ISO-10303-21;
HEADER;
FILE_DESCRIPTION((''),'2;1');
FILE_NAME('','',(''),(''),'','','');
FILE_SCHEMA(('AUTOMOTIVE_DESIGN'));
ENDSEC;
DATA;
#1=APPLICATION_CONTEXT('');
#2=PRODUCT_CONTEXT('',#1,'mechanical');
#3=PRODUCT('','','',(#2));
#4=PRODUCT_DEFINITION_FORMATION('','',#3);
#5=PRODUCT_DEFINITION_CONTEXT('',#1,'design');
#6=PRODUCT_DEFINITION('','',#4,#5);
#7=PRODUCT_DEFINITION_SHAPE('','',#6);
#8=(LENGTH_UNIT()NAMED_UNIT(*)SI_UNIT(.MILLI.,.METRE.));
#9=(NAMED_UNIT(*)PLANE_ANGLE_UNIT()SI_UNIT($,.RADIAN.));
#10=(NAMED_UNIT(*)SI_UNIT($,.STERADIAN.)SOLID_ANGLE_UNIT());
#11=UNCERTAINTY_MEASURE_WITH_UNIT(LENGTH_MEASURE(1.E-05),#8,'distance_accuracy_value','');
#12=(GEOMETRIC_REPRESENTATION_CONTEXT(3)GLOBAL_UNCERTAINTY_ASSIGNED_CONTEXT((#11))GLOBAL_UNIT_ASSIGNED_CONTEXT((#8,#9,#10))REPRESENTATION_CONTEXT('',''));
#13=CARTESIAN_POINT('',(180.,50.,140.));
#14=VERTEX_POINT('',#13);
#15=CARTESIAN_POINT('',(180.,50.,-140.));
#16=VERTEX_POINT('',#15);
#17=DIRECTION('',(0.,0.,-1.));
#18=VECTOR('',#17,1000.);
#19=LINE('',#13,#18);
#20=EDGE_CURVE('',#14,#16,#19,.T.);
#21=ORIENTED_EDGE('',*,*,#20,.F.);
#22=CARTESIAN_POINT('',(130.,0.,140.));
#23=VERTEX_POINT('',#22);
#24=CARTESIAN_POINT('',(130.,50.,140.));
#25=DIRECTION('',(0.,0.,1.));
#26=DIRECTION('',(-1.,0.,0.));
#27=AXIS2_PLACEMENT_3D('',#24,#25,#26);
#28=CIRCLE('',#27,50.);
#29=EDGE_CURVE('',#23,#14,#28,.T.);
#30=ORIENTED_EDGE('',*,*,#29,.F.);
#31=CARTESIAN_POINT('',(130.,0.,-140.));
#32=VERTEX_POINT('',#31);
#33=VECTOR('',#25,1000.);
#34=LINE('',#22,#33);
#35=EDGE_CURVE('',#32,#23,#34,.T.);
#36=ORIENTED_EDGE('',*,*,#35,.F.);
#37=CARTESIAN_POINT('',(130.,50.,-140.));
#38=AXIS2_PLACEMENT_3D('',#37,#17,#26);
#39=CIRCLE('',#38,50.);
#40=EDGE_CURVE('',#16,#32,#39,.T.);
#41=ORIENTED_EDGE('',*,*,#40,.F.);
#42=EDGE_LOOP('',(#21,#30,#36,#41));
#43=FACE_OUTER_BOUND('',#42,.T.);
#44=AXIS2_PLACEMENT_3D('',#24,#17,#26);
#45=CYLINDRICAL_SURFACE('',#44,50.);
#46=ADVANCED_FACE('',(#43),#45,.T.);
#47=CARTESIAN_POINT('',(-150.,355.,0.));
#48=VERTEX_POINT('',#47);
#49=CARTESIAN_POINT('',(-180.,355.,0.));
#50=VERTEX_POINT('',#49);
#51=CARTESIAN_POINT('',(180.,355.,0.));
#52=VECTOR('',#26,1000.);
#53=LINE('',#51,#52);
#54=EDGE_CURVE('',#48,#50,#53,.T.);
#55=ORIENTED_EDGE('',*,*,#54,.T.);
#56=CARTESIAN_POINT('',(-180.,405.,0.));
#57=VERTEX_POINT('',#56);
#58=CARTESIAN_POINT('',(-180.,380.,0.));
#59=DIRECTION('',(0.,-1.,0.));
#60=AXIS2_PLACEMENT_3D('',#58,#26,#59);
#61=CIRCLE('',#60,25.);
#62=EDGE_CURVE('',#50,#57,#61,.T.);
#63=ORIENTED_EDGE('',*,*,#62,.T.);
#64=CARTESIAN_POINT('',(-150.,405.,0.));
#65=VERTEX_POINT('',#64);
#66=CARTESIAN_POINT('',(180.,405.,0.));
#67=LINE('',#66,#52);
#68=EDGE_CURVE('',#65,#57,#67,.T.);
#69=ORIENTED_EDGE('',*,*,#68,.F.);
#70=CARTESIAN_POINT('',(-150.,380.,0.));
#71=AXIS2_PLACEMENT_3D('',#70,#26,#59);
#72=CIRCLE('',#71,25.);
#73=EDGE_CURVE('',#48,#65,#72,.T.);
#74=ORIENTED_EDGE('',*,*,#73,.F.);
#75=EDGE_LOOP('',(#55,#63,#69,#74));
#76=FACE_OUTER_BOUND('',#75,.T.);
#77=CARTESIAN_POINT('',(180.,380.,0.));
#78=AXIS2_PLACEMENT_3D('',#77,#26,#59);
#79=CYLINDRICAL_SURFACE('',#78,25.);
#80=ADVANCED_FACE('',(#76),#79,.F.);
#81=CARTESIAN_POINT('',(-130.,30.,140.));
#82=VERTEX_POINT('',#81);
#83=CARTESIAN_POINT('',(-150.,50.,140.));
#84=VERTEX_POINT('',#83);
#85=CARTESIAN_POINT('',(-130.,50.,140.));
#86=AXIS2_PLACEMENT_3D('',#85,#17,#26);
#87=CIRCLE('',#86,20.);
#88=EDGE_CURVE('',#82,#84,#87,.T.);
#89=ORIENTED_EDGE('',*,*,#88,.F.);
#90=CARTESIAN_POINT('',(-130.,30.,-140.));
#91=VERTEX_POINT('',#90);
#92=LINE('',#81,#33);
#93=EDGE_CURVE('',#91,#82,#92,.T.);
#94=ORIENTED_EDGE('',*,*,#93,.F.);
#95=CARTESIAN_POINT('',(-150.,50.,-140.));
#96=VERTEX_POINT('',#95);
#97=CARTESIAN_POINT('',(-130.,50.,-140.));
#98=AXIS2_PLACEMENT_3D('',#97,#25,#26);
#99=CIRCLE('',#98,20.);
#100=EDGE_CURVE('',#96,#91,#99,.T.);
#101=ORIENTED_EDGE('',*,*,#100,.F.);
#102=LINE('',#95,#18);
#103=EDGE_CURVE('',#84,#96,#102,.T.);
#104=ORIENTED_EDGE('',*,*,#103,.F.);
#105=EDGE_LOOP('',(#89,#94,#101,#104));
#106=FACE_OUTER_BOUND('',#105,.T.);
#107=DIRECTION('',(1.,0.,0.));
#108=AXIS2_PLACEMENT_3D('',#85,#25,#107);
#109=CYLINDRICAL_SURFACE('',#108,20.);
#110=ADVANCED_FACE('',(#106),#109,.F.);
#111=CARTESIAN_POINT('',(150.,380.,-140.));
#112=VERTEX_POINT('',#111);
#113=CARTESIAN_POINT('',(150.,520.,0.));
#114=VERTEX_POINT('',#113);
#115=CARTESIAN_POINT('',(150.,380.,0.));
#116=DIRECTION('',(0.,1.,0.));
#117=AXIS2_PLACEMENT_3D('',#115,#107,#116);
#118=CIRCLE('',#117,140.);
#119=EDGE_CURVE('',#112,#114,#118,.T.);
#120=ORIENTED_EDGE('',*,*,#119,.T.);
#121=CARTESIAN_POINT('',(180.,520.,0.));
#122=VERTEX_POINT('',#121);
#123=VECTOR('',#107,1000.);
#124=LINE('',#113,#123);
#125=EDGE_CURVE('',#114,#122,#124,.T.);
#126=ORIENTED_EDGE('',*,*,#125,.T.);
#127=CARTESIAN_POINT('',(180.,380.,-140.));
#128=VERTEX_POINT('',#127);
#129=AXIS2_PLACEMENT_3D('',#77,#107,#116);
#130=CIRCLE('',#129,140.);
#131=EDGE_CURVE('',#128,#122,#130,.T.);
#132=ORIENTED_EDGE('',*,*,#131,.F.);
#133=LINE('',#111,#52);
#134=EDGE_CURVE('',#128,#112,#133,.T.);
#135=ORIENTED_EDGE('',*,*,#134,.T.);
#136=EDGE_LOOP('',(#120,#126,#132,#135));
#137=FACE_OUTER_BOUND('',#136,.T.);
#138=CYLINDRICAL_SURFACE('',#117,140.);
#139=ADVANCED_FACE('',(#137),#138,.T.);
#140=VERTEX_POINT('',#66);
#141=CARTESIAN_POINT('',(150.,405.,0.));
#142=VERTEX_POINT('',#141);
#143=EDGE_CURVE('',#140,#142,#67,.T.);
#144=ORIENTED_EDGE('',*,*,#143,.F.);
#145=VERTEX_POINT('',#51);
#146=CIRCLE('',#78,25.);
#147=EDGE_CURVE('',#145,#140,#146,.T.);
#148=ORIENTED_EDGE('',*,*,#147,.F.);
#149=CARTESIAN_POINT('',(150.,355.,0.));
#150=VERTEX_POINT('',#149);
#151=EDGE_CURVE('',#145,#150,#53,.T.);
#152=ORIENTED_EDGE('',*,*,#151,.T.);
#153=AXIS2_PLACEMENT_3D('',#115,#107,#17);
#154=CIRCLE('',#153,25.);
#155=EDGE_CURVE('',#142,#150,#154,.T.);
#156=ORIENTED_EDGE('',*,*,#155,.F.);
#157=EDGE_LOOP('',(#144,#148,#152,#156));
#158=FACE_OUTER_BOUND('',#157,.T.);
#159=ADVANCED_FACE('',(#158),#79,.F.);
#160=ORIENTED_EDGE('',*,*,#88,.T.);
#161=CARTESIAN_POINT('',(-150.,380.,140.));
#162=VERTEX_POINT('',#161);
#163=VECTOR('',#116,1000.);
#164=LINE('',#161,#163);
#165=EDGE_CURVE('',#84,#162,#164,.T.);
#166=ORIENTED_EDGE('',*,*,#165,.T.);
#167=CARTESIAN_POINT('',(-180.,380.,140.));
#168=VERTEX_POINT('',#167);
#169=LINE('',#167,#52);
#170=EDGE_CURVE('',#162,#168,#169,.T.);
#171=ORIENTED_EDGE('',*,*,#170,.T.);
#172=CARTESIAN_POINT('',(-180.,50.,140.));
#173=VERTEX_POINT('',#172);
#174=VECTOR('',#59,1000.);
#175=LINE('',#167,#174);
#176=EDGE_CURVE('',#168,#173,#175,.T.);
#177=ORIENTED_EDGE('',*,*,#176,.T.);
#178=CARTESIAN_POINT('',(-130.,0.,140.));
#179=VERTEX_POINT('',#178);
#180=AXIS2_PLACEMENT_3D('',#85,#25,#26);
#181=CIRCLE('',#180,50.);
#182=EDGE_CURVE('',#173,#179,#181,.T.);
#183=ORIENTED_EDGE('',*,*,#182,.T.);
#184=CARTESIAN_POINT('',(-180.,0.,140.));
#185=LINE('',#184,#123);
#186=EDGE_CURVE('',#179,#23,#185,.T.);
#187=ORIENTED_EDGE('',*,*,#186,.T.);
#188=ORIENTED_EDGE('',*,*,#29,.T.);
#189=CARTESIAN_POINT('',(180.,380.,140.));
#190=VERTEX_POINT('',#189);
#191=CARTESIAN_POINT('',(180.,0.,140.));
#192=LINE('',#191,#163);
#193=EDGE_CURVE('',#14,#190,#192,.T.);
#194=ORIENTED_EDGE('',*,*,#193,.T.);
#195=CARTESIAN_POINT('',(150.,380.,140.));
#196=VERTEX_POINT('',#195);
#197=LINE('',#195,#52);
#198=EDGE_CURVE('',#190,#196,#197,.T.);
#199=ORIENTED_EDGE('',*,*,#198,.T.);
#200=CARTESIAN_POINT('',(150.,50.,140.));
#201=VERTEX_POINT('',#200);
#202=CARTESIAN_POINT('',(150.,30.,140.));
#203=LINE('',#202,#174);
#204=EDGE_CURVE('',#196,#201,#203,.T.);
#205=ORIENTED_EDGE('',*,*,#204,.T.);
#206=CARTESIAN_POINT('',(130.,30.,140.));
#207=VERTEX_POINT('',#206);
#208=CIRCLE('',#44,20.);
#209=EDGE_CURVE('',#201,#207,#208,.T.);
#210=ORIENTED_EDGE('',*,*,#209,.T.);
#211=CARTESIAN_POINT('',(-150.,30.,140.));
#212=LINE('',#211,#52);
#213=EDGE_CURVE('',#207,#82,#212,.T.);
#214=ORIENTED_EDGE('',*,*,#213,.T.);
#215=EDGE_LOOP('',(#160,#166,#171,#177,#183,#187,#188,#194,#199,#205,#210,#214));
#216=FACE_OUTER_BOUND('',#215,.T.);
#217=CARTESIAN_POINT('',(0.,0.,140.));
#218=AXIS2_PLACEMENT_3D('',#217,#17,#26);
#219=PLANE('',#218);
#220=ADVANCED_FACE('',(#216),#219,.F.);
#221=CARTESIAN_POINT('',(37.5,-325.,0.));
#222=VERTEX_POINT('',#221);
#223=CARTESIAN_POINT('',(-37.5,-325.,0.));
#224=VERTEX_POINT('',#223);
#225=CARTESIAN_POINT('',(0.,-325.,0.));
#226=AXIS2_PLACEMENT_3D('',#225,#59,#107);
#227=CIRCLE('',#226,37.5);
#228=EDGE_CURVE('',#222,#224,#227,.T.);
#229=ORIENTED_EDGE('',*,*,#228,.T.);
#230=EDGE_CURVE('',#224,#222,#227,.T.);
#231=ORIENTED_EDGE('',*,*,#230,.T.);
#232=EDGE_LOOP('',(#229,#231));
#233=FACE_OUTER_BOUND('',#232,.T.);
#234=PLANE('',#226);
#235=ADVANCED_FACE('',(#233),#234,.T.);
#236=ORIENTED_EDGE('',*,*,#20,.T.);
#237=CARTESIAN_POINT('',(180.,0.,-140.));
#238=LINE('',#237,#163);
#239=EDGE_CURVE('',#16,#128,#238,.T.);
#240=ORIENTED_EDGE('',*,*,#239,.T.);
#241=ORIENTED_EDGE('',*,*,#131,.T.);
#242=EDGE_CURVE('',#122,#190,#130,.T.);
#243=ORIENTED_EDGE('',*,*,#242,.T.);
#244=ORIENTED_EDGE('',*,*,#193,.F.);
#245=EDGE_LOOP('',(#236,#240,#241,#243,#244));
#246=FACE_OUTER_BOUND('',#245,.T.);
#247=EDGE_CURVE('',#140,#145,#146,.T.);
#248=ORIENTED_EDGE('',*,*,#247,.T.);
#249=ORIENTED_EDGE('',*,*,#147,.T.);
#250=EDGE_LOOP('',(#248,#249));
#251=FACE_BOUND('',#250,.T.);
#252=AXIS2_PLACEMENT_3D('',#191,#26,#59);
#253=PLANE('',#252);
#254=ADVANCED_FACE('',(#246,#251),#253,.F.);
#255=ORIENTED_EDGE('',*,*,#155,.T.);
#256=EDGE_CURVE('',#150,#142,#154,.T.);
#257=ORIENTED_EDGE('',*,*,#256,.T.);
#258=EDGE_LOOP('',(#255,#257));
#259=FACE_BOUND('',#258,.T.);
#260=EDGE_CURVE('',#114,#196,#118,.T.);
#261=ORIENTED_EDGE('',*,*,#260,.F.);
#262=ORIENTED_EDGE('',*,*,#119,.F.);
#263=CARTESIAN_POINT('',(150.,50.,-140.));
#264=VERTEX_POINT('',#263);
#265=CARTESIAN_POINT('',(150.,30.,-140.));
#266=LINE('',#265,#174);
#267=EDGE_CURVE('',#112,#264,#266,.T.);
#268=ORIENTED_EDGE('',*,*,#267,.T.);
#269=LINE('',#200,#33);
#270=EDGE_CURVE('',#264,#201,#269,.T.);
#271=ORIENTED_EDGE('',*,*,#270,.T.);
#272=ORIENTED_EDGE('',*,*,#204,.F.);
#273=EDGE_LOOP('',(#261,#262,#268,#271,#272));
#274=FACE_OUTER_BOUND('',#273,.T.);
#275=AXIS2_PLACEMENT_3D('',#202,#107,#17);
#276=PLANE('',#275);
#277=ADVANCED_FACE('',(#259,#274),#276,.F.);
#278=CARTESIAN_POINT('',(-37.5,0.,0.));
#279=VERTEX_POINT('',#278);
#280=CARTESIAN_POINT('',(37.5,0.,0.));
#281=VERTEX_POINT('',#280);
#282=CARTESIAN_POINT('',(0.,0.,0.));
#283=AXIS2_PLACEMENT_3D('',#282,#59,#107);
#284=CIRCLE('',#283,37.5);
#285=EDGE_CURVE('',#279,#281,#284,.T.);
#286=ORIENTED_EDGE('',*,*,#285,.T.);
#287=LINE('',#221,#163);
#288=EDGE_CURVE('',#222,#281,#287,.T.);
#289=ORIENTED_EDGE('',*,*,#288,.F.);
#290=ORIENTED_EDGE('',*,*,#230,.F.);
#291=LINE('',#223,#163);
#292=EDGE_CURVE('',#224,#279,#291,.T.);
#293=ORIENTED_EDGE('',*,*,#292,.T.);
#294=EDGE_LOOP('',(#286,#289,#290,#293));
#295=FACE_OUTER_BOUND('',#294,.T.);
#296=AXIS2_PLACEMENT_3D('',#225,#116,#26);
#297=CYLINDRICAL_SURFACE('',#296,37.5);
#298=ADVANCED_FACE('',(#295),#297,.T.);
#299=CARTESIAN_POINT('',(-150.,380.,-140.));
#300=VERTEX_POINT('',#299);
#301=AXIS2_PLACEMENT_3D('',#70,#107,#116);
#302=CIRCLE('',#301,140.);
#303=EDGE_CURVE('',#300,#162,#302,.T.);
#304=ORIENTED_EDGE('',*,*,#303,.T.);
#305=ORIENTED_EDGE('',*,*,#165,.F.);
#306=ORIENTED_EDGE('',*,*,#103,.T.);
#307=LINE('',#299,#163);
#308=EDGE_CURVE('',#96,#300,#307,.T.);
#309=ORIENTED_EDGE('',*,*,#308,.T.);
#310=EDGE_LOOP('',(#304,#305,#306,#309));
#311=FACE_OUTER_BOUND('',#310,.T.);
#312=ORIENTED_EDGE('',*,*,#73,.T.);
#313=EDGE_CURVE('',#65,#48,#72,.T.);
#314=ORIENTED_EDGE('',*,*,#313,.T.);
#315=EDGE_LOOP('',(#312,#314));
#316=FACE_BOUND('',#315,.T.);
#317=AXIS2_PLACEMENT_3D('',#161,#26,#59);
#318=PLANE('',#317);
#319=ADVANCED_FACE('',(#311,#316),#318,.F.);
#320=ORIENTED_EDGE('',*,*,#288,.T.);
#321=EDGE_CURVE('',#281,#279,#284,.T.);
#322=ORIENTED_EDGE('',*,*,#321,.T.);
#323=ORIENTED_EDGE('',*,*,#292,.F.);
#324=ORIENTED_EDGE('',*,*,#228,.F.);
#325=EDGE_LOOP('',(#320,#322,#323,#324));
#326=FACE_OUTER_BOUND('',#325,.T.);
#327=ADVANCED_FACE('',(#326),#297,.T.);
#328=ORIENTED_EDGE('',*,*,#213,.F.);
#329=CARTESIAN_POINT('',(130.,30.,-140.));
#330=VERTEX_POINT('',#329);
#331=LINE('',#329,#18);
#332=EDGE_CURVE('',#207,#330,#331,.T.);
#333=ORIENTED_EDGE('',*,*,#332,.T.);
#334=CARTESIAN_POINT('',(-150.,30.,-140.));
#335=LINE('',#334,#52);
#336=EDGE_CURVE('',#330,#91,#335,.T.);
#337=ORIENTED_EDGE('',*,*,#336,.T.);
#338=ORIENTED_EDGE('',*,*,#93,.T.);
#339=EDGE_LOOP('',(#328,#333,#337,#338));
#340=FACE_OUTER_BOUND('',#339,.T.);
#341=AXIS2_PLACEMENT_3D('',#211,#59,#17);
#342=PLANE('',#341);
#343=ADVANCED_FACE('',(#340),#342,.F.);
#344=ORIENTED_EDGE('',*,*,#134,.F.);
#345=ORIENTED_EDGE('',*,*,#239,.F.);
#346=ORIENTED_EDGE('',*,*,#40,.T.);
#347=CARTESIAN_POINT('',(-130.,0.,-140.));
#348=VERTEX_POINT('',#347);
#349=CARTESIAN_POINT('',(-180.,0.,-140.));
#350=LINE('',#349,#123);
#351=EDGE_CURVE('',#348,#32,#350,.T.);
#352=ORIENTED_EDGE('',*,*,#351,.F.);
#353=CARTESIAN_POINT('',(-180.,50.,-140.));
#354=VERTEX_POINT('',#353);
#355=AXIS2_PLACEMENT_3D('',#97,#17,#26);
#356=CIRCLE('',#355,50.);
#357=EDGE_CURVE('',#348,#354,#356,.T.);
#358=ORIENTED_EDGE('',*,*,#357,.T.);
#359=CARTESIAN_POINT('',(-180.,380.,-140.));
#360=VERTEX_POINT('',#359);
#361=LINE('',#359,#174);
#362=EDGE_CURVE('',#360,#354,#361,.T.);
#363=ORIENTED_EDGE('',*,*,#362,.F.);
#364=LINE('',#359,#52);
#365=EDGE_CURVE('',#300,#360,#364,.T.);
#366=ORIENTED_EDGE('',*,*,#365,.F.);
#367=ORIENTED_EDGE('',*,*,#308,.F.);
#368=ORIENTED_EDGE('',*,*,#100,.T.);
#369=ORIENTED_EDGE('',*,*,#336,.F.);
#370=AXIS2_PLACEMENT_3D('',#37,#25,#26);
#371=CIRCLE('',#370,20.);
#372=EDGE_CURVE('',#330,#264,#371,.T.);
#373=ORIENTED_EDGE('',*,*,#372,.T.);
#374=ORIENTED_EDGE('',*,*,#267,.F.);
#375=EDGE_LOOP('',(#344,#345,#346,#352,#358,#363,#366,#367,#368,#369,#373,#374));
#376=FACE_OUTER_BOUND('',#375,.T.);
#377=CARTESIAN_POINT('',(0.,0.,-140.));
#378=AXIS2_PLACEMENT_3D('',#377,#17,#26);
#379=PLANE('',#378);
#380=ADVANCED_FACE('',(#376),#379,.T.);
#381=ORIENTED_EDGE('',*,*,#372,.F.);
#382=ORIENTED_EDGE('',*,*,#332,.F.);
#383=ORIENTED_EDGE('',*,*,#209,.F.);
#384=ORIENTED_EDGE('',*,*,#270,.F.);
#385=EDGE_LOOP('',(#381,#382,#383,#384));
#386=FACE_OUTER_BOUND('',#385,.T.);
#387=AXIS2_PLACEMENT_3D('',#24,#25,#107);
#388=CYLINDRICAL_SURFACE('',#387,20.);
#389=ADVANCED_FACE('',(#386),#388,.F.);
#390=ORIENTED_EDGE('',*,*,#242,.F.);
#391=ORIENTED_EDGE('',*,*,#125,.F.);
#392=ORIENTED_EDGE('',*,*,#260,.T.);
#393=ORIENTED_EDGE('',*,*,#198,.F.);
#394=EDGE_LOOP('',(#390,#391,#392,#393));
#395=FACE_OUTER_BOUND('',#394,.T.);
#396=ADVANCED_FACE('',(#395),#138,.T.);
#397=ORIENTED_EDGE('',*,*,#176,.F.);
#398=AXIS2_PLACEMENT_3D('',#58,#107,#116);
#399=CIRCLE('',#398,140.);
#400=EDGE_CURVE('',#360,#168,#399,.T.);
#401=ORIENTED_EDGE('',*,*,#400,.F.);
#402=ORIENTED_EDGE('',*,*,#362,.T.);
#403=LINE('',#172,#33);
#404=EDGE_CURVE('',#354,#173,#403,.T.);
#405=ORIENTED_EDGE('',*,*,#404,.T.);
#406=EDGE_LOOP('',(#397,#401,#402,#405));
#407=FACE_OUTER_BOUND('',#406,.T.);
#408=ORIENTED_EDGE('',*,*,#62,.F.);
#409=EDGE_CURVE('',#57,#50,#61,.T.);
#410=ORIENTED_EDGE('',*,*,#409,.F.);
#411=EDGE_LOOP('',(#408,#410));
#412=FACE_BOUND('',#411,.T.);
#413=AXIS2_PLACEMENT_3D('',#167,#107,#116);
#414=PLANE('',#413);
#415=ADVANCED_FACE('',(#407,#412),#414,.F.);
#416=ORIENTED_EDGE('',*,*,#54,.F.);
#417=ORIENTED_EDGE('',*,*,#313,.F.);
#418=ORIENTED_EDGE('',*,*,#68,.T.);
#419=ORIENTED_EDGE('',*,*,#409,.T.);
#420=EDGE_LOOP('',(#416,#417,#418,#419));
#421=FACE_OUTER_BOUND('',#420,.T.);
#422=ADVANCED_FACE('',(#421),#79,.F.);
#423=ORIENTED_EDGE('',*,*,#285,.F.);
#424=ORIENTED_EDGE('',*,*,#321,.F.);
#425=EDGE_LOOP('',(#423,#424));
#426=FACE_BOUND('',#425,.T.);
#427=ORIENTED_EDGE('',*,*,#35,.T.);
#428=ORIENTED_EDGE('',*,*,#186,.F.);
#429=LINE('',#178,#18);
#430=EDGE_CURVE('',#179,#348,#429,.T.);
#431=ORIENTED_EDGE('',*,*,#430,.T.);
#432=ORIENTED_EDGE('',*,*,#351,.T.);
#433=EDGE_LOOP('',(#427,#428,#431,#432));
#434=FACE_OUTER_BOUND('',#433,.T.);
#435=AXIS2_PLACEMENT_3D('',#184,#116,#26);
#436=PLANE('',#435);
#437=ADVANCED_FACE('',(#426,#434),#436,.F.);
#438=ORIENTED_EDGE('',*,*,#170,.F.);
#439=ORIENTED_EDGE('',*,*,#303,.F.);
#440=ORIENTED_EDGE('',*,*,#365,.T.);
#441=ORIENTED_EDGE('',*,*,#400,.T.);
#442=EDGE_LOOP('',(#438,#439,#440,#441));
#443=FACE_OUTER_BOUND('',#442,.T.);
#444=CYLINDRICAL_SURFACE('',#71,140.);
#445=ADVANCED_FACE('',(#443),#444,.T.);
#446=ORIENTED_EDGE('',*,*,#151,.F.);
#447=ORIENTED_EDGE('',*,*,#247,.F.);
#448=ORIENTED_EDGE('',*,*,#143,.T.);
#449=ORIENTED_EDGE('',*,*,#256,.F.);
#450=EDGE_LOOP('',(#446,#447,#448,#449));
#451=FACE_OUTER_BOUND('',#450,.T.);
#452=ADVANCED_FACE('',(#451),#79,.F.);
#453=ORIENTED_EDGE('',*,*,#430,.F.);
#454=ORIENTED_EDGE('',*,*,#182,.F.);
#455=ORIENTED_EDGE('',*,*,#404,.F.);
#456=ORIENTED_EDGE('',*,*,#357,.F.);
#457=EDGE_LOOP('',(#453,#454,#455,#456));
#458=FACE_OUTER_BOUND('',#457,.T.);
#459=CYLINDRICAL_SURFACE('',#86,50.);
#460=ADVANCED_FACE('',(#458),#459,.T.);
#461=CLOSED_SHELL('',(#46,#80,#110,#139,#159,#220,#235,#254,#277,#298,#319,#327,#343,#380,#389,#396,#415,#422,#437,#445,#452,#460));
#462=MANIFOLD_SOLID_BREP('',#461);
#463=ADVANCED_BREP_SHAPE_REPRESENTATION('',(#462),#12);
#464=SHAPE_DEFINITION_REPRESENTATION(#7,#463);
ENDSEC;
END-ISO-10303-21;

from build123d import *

# Parameters (mm, degrees)
U_CHANNEL_BODY_DEPTH     = 140
STEM_SKETCH_75_R         = 37.5
STEM_75_DEPTH            = 325
UPRIGHT_TOP_ROUNDS_R50_R = 50
CHANNEL_FILLETS_R20_R    = 20
SIDE_BOSS_SKETCH_R       = 140
SIDE_BOSS_DEPTH          = 30
PIN_HOLE_SKETCH_R        = 25
PIN_HOLES_DEPTH          = 648.765389628


with BuildPart() as part:
    # U-Channel Profile Sketch → U-Channel Body (new, symmetric)
    with BuildSketch(Plane.XY):
        Polygon((-180, 380), (-180, 0), (180, 0), (180, 380), (150, 380), (150, 30), (-150, 30), (-150, 380), align=None)
    extrude(amount=U_CHANNEL_BODY_DEPTH, both=True)

    # Stem Sketch Ø75 → Stem Ø75 (add)
    with BuildSketch(Plane.XZ):
        Circle(STEM_SKETCH_75_R)
    extrude(amount=STEM_75_DEPTH)

    # Upright Top Rounds R50
    upright_top_rounds_r50_edges = [part.edges().sort_by_distance(p)[0] for p in [
        (180, 0, 0),
        (-180, 0, 0),
    ]]
    fillet(upright_top_rounds_r50_edges, radius=UPRIGHT_TOP_ROUNDS_R50_R)

    # Channel Fillets R20
    channel_fillets_r20_edges = [part.edges().sort_by_distance(p)[0] for p in [
        (-150, 30, 0),
        (150, 30, 0),
    ]]
    fillet(channel_fillets_r20_edges, radius=CHANNEL_FILLETS_R20_R)

    # Side Boss Sketch → Side Boss (add)
    with BuildSketch(Plane(origin=(180, 0, 0), x_dir=(0, 0, -1), z_dir=(1, 0, 0))):
        with Locations((0, 380)):
            Circle(SIDE_BOSS_SKETCH_R)
    side_boss = extrude(amount=-SIDE_BOSS_DEPTH)

    # Side Boss Mirror: Side Boss across plane
    add(side_boss.mirror(Plane(origin=(0, 0, 0), x_dir=(0, 0, 1), z_dir=(1, 0, 0))))

    # Pin Hole Sketch → Pin Holes (cut, through all)
    with BuildSketch(Plane.ZY.offset(180)):
        with Locations(Location((0, 380, 0), (0, 0, 270))):
            Circle(PIN_HOLE_SKETCH_R)
    extrude(amount=-PIN_HOLES_DEPTH, mode=Mode.SUBTRACT)


solid = part.part
